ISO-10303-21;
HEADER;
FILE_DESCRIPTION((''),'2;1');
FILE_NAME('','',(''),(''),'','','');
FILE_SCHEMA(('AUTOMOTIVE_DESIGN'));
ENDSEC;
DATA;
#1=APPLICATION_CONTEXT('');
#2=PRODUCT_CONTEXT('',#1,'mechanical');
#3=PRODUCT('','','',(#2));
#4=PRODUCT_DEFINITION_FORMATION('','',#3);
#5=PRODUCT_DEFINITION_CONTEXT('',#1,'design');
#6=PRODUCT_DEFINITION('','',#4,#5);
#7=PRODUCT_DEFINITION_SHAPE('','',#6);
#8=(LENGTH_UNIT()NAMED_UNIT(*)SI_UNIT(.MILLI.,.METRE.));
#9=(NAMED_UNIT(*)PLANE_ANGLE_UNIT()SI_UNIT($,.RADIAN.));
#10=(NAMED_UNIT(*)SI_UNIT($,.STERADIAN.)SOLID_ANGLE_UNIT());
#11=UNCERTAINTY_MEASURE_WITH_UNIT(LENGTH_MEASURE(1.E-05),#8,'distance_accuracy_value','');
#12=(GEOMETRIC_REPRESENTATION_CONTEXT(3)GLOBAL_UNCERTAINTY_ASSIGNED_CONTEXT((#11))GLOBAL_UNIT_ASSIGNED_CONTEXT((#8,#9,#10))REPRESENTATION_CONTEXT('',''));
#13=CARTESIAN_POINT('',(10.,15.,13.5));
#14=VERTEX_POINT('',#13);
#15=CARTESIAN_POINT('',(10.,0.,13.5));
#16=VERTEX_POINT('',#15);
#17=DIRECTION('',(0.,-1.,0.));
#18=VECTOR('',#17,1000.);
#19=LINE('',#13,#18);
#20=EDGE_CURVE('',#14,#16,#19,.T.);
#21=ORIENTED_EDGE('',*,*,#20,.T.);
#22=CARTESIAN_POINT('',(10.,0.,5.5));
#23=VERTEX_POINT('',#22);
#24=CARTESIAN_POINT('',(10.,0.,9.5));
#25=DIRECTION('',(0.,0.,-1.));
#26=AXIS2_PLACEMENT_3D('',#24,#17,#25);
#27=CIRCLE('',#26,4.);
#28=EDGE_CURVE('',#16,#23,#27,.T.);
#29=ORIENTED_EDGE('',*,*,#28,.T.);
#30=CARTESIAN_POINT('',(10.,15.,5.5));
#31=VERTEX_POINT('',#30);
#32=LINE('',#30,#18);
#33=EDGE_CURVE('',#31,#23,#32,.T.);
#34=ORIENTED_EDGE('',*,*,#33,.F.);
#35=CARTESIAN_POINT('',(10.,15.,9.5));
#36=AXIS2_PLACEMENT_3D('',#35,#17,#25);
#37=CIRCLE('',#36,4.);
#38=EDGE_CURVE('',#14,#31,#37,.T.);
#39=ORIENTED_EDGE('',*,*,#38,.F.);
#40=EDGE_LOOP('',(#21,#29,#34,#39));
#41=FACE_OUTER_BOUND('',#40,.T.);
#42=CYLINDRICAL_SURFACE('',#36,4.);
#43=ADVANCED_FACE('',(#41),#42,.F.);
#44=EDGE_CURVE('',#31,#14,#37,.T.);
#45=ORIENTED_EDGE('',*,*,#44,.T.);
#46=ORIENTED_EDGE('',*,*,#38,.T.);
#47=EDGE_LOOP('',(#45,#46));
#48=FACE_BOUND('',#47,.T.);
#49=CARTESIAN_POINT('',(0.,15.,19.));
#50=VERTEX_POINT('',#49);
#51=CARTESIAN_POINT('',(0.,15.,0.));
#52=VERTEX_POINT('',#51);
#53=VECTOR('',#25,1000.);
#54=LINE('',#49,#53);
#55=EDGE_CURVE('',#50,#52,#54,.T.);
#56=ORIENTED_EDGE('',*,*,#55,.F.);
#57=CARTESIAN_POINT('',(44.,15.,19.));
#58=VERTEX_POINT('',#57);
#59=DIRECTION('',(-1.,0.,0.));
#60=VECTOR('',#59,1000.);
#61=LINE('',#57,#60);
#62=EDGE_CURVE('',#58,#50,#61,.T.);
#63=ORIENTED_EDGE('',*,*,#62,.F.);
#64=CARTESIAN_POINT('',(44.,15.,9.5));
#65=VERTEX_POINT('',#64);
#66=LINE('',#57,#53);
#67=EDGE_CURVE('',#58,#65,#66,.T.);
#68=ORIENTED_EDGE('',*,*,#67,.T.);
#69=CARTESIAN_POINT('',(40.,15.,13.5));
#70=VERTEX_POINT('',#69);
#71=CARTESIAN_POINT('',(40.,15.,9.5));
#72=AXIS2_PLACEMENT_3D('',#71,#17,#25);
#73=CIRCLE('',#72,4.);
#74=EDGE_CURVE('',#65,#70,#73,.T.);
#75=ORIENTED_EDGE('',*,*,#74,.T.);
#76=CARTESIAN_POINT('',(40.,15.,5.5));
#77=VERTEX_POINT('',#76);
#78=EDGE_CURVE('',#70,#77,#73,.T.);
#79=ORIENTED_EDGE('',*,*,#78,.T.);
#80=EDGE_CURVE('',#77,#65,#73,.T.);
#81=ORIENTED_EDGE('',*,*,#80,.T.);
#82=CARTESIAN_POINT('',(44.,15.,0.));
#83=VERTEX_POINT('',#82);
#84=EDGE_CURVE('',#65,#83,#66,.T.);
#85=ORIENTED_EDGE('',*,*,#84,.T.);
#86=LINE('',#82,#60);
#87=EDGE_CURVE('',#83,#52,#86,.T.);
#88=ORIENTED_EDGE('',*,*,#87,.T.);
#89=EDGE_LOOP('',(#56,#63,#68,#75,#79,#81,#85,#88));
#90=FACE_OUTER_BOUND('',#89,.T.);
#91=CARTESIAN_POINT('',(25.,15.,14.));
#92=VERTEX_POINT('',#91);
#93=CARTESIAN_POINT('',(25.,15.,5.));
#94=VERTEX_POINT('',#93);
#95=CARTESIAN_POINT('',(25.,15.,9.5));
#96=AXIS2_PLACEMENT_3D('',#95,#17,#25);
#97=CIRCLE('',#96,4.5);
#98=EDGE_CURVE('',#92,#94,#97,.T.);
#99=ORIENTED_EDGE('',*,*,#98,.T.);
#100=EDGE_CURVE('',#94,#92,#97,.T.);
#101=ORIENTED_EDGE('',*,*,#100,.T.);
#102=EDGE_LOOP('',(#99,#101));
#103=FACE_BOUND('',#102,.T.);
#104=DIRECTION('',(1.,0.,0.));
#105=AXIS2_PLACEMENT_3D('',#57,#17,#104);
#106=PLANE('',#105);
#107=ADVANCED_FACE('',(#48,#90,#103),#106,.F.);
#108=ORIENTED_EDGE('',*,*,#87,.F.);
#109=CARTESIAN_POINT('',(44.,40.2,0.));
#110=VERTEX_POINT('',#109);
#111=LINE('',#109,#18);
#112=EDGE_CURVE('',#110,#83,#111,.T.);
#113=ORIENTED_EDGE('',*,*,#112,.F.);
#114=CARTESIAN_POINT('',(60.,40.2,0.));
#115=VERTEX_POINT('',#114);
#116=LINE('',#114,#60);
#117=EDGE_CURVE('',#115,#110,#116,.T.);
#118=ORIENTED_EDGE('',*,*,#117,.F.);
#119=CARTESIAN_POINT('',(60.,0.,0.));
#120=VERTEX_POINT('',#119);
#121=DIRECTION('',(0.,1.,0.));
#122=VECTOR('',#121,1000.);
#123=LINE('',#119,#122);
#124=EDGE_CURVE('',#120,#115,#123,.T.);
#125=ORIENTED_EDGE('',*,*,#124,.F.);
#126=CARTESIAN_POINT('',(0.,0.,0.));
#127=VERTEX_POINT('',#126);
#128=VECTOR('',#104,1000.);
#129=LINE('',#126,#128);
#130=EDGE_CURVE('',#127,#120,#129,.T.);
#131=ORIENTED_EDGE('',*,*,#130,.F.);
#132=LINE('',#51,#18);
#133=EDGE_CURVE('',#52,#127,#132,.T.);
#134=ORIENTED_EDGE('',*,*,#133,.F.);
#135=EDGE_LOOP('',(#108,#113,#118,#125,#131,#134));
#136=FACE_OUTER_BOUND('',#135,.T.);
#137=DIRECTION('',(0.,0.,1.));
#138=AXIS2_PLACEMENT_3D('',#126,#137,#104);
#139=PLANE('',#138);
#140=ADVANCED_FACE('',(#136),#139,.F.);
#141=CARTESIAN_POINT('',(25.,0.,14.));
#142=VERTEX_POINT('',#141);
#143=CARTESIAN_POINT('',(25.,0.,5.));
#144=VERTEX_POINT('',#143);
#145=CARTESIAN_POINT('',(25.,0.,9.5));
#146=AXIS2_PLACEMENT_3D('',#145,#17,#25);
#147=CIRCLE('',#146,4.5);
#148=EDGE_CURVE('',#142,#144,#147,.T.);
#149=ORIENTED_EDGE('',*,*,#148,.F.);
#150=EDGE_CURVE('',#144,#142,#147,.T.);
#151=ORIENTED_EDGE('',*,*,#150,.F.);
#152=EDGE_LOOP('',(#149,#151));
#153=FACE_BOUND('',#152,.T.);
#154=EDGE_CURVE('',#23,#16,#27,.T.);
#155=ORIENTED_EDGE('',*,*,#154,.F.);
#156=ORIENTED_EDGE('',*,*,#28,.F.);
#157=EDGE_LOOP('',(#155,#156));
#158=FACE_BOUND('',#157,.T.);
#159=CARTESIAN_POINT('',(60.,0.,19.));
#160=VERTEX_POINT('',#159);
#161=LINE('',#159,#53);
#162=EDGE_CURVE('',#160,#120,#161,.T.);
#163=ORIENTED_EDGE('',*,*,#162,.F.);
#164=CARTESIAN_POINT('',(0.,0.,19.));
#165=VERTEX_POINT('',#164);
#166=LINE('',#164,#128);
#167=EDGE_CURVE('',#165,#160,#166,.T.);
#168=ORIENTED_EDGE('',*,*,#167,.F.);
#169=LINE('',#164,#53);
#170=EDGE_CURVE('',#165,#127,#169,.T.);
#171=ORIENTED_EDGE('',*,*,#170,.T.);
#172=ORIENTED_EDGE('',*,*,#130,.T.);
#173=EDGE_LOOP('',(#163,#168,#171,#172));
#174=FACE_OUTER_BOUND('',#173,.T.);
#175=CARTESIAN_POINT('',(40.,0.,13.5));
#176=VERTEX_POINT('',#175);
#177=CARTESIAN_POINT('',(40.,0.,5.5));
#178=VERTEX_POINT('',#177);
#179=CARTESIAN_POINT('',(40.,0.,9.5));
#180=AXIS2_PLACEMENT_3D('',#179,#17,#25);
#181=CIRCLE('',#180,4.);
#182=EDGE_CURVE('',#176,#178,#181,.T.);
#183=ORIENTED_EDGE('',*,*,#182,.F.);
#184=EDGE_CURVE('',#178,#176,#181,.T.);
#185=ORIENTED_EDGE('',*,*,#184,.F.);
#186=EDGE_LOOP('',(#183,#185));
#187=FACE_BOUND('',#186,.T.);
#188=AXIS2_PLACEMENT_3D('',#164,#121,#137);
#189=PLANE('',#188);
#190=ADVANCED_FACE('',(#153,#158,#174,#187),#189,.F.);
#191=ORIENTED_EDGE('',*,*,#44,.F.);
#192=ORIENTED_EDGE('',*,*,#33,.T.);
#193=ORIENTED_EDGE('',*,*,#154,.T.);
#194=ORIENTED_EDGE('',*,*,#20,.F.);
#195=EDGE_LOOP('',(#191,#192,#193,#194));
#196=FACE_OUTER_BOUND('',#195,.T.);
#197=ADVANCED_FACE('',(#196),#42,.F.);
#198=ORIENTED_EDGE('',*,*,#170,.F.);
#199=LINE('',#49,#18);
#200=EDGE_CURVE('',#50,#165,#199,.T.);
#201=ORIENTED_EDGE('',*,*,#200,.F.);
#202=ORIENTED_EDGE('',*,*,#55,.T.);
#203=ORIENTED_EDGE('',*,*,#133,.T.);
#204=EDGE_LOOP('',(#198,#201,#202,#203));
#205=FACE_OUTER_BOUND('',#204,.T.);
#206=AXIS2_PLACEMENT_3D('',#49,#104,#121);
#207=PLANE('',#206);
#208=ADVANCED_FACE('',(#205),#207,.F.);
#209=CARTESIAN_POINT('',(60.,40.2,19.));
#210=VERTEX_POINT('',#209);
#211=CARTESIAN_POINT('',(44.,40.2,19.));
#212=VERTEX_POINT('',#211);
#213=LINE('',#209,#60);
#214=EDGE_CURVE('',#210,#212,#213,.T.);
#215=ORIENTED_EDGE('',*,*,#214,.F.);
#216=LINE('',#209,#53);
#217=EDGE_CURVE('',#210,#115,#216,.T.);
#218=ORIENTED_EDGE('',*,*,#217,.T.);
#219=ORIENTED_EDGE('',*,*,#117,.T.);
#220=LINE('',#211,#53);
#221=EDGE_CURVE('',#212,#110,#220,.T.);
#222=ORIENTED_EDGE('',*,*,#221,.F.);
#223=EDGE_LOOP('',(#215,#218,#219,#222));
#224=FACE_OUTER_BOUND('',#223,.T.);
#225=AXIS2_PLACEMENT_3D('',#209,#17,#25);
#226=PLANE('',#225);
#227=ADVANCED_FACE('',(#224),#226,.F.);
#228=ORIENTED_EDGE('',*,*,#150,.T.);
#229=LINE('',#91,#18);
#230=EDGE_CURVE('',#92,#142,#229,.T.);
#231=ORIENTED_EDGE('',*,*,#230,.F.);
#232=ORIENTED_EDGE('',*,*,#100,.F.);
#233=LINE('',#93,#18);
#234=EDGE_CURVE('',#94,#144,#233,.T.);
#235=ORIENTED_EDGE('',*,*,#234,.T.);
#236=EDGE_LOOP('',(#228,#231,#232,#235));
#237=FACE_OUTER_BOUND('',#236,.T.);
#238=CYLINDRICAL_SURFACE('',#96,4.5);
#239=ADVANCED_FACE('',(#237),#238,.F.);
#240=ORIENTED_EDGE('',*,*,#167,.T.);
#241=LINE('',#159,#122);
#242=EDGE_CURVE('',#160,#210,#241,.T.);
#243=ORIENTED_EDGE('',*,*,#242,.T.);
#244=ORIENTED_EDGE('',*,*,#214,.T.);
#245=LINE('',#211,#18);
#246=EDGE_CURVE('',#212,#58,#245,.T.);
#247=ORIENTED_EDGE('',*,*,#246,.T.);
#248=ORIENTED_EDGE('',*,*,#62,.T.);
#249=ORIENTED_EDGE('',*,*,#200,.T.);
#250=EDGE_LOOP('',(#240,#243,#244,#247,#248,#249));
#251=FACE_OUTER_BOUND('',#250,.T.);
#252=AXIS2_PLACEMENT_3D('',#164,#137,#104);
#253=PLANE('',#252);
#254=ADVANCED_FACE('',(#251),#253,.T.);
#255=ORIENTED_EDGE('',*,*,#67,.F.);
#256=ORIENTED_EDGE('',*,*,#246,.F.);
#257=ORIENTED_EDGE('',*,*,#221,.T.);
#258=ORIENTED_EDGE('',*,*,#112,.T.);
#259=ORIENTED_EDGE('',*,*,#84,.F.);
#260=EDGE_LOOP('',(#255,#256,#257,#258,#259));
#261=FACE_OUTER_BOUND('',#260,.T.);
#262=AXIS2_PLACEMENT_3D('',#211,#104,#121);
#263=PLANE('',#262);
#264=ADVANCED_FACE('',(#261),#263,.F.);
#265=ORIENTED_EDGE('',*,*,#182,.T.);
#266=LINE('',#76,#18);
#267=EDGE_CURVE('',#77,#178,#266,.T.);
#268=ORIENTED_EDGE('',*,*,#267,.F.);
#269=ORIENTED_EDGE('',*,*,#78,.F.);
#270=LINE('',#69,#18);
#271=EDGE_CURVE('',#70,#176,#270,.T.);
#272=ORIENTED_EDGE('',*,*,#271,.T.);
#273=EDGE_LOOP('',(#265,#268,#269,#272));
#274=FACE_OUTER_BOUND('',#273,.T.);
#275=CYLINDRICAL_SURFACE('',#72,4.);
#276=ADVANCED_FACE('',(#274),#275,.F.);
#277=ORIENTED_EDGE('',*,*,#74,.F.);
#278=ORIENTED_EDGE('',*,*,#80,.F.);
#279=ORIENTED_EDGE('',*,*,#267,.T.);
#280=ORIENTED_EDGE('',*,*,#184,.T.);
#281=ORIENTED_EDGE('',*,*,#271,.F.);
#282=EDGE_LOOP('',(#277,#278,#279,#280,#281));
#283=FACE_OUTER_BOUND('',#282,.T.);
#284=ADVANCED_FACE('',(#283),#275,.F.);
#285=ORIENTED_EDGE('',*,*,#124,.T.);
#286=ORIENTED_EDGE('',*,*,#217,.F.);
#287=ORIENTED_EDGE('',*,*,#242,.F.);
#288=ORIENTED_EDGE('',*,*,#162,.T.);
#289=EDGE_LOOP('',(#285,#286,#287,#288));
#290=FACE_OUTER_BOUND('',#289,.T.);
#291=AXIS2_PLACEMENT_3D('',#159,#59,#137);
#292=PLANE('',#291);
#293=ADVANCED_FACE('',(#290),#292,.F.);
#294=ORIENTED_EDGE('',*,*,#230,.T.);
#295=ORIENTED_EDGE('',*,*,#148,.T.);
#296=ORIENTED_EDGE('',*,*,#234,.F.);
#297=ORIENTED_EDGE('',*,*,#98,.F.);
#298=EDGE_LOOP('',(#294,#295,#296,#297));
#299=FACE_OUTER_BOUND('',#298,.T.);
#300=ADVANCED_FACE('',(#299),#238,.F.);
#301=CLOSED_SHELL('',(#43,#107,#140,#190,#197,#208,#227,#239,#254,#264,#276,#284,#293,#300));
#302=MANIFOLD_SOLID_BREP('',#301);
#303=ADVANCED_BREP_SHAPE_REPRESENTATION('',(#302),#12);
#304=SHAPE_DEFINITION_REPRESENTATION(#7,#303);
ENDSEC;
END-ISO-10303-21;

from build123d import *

# Parameters (mm, degrees)
BOSS_EXTRUDE1_DEPTH = 19
SKETCH2_R           = 4
SKETCH2_R_2         = 4.5
CUT_EXTRUDE1_DEPTH  = 15


with BuildPart() as part:
    # Sketch1 → Boss-Extrude1 (new body)
    with BuildSketch(Plane.XY):
        Polygon((0, 0), (60, 0), (60, 40.20000018), (44, 40.20000018), (44, 15), (0, 15), align=None)
    extrude(amount=BOSS_EXTRUDE1_DEPTH)

    # Sketch2 → Cut-Extrude1 (cut)
    with BuildSketch(Plane(origin=(0, 0, 0), x_dir=(-1, 0, 0), z_dir=(0, -1, 0))):
        with Locations(Location((-10, -9.5, 0), (0, 0, 90))):
            Circle(SKETCH2_R)
        with Locations(Location((-25, -9.5, 0), (0, 0, 90))):
            Circle(SKETCH2_R_2)
        with Locations(Location((-40, -9.5, 0), (0, 0, 90))):
            Circle(SKETCH2_R)
    extrude(amount=-CUT_EXTRUDE1_DEPTH, mode=Mode.SUBTRACT)


solid = part.part
